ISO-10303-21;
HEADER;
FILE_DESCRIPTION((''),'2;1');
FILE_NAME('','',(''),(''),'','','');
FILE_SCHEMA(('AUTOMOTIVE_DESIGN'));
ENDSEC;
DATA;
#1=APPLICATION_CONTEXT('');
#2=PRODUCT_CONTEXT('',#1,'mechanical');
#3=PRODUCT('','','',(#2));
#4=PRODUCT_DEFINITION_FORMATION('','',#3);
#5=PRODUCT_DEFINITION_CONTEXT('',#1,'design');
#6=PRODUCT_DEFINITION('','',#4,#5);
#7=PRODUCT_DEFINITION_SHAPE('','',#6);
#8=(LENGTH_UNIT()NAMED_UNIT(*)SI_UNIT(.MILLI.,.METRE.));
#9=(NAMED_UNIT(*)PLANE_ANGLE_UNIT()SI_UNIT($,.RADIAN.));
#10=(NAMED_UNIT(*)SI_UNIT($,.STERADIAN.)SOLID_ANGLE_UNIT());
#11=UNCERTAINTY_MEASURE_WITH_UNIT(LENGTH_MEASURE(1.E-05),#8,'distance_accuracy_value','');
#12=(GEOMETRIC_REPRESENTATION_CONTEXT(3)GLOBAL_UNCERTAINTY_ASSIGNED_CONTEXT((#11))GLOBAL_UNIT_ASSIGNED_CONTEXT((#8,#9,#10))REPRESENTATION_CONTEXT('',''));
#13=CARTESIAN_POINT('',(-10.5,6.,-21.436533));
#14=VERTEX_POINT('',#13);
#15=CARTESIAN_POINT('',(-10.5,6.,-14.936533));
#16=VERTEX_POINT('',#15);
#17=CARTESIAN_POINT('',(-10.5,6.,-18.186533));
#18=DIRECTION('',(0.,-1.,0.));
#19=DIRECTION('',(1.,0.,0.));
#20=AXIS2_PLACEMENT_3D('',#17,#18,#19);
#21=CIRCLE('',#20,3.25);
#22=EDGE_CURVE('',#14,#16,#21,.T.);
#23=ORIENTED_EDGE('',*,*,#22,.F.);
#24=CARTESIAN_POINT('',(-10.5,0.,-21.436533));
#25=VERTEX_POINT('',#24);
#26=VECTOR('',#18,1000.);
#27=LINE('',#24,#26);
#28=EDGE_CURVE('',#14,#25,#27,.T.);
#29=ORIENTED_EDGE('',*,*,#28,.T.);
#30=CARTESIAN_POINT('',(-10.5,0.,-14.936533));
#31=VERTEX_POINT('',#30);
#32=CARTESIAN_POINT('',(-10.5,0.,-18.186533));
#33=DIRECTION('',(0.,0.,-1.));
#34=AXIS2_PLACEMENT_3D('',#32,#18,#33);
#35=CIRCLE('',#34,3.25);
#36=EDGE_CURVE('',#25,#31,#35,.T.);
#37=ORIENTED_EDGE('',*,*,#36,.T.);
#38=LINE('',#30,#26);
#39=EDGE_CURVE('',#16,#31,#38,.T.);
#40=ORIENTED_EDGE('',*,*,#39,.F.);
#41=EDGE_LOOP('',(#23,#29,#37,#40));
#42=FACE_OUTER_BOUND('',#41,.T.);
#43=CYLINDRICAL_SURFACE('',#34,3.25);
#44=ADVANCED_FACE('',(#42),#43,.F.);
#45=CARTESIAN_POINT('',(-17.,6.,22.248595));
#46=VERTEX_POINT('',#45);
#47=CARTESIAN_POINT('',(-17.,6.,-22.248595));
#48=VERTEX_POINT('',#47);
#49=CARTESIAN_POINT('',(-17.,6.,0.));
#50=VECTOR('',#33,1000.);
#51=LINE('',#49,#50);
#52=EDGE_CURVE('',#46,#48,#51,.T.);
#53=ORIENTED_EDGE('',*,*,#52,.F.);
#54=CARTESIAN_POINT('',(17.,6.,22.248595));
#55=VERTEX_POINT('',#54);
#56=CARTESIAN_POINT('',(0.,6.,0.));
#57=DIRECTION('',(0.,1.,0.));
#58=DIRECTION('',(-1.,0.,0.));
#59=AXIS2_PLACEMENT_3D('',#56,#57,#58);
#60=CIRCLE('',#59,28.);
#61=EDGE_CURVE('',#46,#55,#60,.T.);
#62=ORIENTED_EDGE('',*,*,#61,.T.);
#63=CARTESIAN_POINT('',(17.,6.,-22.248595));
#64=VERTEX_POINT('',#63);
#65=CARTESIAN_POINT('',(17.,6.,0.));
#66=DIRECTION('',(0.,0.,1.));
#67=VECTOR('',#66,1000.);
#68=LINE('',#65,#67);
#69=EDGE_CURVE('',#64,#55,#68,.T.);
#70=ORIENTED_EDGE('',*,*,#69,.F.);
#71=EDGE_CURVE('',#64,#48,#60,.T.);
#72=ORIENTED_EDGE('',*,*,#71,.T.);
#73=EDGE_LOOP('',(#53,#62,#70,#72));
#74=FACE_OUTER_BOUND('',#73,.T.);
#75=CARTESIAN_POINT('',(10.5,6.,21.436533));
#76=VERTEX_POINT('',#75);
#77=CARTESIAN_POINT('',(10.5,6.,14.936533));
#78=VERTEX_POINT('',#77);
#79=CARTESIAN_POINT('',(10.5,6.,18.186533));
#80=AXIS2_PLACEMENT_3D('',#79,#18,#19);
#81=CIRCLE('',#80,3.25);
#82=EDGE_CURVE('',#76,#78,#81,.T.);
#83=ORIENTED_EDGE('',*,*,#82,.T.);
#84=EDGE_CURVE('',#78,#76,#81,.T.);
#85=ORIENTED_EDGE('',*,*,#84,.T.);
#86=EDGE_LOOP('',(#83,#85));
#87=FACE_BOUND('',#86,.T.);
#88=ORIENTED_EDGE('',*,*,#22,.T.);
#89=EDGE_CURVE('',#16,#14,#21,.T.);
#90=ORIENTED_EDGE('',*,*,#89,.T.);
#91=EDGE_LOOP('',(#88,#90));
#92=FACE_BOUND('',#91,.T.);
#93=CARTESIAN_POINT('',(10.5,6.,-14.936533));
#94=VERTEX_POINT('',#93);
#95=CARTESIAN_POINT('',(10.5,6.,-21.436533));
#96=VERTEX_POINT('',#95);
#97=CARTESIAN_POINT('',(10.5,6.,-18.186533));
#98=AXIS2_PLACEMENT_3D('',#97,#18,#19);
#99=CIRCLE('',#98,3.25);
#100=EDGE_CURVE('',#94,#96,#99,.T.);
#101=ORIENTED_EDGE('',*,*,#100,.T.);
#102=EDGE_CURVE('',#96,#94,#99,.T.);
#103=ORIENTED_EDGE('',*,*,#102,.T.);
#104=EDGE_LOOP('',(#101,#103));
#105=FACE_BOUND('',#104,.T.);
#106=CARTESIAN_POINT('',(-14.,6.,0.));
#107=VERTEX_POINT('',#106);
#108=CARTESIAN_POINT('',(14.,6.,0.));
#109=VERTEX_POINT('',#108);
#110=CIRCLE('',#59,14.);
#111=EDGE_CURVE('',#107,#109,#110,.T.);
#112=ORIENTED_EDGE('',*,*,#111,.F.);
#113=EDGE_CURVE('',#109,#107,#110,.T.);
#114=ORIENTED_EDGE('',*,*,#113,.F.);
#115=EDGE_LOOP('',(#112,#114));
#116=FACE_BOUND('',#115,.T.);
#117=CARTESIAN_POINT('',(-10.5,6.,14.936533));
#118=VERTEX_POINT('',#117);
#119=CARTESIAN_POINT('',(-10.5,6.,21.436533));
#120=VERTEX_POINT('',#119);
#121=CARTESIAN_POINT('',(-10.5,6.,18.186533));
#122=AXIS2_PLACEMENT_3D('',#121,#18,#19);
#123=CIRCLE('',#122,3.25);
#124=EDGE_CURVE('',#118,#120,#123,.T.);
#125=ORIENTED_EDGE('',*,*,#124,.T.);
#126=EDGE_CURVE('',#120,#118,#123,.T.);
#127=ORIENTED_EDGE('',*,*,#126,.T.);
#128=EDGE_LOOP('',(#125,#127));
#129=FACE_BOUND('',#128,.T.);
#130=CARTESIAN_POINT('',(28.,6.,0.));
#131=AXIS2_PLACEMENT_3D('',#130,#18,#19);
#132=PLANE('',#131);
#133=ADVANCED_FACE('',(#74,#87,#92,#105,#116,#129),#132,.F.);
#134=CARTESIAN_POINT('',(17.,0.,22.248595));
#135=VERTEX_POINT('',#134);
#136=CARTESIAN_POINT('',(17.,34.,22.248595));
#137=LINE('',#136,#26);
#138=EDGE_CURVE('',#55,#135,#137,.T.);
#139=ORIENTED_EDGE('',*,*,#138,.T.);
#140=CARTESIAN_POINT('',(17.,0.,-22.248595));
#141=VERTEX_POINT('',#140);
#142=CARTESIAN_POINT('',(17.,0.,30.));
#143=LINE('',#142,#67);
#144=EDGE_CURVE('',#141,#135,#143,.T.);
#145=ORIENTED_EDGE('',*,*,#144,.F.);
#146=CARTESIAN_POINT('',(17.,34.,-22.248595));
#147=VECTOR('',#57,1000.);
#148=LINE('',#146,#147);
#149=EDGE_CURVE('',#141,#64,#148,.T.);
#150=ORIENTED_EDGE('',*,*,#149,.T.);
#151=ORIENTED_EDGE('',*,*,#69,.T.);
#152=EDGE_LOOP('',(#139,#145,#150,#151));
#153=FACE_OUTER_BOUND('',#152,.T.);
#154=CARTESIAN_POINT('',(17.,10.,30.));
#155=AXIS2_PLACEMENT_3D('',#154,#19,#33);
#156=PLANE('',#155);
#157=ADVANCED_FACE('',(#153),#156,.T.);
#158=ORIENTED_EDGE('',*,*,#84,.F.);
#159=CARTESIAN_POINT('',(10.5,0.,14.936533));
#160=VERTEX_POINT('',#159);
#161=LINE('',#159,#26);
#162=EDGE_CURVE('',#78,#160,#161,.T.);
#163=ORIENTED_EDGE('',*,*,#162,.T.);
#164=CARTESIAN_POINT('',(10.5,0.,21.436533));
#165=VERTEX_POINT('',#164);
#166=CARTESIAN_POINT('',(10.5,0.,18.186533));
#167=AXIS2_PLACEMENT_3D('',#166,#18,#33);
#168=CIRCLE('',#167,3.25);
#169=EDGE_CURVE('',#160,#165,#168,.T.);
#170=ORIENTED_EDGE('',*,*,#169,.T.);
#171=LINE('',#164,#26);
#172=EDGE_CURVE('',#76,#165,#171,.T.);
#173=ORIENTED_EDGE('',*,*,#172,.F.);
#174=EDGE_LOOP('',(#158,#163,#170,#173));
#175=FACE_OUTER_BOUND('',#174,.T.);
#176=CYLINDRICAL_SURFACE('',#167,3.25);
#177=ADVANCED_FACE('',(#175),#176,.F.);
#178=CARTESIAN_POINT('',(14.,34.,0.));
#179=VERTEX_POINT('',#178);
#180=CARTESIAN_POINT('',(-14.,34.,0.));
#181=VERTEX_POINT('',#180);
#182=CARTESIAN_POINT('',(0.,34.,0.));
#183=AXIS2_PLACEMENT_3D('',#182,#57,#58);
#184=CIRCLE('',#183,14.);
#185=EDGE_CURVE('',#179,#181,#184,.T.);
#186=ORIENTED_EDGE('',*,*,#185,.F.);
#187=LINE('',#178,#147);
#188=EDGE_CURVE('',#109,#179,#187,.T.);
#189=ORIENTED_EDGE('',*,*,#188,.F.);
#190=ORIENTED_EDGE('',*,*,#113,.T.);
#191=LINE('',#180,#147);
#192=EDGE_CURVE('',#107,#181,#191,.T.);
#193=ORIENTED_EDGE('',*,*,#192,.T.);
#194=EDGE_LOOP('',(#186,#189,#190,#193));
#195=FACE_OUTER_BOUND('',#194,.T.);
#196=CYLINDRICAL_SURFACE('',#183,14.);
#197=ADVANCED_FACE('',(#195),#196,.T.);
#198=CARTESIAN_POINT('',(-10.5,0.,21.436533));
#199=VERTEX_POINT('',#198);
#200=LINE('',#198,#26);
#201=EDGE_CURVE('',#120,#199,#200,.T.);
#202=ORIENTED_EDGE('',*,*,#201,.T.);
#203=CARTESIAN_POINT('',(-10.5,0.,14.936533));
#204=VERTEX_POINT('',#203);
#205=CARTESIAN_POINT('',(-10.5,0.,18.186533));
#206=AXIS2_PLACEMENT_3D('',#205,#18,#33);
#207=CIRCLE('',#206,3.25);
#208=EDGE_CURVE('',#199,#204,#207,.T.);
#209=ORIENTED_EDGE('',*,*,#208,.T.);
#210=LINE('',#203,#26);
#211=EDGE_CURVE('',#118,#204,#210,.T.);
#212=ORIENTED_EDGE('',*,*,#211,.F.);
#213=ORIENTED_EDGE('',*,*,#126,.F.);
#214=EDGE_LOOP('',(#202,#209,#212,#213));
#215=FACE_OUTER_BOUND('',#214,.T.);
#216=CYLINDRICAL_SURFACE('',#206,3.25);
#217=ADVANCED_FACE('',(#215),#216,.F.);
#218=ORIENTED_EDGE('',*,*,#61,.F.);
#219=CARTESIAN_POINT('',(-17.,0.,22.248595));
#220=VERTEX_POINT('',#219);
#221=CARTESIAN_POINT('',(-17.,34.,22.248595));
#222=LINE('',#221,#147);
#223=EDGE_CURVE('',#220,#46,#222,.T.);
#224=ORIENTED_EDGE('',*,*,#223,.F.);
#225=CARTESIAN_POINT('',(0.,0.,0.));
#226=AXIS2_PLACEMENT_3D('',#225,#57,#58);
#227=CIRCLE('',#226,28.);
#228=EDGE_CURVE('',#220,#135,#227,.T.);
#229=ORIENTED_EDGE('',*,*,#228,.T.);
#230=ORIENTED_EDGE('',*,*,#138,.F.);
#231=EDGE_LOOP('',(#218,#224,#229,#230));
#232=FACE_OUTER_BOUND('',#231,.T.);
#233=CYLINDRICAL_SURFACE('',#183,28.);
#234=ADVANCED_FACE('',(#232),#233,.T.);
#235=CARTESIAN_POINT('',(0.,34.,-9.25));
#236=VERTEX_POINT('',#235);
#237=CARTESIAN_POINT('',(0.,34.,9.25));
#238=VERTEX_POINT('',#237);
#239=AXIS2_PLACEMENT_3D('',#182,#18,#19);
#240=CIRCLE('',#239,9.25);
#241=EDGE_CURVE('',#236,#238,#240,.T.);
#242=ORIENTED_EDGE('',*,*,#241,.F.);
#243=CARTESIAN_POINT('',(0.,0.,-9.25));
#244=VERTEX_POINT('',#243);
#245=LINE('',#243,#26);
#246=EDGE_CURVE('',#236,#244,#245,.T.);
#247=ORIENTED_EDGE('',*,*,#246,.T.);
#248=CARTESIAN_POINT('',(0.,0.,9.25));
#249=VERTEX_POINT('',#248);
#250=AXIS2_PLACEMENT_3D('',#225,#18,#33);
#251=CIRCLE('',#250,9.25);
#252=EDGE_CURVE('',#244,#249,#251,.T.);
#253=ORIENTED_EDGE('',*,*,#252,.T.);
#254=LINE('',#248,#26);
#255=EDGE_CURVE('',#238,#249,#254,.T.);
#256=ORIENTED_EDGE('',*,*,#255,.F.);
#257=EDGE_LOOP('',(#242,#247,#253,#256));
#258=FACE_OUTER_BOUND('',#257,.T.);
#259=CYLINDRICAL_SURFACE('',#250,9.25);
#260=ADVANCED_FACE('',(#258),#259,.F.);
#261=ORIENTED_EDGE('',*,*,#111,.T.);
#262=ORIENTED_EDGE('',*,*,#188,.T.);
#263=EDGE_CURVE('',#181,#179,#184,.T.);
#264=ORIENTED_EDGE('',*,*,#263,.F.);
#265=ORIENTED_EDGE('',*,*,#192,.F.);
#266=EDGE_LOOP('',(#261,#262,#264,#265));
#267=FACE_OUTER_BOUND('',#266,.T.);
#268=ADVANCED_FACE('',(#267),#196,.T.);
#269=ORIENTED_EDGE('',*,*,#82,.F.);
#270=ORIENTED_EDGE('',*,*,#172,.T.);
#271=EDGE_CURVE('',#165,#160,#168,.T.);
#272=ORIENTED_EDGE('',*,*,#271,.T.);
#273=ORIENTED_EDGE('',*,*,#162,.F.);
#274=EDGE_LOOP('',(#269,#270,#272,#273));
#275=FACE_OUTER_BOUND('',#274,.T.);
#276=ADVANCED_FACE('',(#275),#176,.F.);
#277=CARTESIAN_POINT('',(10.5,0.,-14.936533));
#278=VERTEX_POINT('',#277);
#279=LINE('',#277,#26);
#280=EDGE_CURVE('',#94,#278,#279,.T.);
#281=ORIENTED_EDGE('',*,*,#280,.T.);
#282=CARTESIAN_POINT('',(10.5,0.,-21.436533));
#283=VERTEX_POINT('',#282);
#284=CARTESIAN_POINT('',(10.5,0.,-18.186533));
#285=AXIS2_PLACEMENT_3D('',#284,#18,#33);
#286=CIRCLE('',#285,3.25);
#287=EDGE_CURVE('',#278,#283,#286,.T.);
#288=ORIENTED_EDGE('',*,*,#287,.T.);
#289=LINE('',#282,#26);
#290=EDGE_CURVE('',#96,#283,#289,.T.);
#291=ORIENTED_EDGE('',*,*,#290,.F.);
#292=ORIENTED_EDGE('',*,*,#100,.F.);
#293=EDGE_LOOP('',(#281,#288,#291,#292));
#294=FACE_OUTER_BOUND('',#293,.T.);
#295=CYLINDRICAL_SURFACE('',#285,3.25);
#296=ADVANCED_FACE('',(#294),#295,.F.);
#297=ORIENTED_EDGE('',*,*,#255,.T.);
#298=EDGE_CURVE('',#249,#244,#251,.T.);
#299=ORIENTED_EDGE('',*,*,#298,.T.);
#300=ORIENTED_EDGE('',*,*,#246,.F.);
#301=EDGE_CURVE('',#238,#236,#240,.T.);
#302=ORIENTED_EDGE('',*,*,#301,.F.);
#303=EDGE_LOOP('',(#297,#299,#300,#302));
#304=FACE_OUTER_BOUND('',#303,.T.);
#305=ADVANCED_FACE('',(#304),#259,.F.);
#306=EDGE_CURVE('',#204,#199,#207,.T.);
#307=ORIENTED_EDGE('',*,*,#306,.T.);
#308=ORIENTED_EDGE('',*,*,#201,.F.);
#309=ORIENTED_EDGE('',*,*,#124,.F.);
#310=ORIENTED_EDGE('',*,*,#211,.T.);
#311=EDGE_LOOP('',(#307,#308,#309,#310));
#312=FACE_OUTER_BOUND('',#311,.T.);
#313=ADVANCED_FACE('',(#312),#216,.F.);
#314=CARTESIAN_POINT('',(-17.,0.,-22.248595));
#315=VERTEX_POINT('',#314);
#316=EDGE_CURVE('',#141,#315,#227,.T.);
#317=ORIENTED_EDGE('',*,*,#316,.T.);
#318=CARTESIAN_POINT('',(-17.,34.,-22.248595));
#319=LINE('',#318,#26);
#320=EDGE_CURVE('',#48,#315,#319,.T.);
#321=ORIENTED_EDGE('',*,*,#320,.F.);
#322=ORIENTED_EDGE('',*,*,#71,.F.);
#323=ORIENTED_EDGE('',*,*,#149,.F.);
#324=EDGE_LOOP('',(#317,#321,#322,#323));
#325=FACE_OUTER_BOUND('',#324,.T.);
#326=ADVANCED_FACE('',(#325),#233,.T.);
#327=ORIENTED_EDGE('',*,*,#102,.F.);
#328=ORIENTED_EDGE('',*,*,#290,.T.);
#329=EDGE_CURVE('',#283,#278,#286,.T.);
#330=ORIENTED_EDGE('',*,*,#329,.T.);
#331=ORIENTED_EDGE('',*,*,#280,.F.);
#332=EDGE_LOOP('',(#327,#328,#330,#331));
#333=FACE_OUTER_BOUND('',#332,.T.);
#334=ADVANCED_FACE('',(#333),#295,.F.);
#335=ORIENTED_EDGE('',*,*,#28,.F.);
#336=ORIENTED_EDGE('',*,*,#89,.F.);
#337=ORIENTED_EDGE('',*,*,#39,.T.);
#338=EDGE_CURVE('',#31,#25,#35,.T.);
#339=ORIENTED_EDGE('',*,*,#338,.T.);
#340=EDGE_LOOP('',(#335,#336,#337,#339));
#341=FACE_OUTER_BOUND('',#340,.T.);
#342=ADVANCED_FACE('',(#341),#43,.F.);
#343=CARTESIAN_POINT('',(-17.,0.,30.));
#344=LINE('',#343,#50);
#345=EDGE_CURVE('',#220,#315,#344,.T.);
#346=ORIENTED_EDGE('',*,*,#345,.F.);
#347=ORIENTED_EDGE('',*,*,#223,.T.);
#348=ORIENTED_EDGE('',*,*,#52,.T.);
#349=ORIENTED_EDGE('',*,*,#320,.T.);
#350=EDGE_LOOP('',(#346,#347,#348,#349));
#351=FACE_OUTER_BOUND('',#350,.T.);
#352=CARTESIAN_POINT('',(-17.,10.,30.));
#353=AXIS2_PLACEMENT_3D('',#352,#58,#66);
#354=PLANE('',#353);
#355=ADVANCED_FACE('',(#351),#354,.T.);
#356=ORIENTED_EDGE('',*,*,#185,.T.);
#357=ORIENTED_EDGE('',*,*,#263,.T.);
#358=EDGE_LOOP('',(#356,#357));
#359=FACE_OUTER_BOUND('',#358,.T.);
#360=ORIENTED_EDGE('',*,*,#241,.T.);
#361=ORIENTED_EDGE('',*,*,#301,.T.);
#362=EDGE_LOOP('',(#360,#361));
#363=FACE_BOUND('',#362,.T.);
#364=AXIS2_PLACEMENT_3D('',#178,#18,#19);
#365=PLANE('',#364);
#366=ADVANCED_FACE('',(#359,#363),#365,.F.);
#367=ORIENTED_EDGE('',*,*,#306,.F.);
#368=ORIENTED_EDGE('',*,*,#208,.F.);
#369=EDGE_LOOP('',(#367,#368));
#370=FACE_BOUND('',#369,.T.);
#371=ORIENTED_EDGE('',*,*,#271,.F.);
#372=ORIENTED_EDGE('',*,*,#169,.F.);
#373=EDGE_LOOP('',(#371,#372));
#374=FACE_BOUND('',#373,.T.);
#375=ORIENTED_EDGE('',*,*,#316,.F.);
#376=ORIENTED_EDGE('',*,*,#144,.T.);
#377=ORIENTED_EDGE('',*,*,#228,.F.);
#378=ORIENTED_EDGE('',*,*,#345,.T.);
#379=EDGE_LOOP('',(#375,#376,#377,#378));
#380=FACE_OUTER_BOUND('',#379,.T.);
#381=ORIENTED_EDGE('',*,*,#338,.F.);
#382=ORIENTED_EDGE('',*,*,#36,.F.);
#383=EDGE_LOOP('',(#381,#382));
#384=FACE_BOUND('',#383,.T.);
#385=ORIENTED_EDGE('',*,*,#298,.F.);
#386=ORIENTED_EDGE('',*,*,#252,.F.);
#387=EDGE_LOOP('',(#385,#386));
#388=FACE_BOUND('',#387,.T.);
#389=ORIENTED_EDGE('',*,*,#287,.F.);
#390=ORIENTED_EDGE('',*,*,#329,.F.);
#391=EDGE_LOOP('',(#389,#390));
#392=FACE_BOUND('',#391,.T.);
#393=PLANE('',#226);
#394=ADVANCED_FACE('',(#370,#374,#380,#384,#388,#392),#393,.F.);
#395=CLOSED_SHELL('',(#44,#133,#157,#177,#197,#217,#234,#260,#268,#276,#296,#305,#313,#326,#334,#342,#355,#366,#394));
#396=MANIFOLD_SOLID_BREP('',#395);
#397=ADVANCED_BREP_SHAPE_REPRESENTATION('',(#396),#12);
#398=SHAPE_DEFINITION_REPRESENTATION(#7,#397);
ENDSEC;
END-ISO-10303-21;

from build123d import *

# Parameters (mm, degrees)
SKETCH2_OUTSIDE_W              = 75.238
SKETCH2_OUTSIDE_H              = 75.238
SKETCH2_OUTSIDE_W_2            = 34
SKETCH2_OUTSIDE_H_2            = 60
CUT_EXTRUDE1_DEPTH             = 10
F_6_5_6_5_DIAMETER_HOLE1_D     = 6.5
F_6_5_6_5_DIAMETER_HOLE1_DEPTH = 20
F_6_5_6_5_DIAMETER_HOLE1_TIP   = 1.952797012
M20X1_5_TAPPED_HOLE1_D         = 18.5
M20X1_5_TAPPED_HOLE1_DEPTH     = 44.5
M20X1_5_TAPPED_HOLE1_TIP       = 5.557960726


with BuildPart() as part:
    # Sketch1 → Revolve1 (revolve)
    with BuildSketch(Plane.XY, mode=Mode.PRIVATE) as revolve1_sk:
        Polygon((0, 0), (28, 0), (28, 6), (14, 6), (14, 34), (0, 34), align=None)
    revolve(revolve1_sk.sketch.rotate(Axis((0, 34, 0), (0, -1, 0)), 180), axis=Axis((0, 34, 0), (0, -1, 0)))

    # Sketch2 outside → Cut-Extrude1 (cut)
    with BuildSketch(Plane.XZ):
        Rectangle(SKETCH2_OUTSIDE_W, SKETCH2_OUTSIDE_H)
        Rectangle(SKETCH2_OUTSIDE_W_2, SKETCH2_OUTSIDE_H_2, mode=Mode.SUBTRACT)
    extrude(amount=-CUT_EXTRUDE1_DEPTH, mode=Mode.SUBTRACT)

    # Ø6.5 (6.5) Diameter Hole1
    with Locations(Plane.XZ):
        with Locations((-10.5, 18.186533479), (10.5, 18.186533479), (-10.5, -18.186533479), (10.5, -18.186533479)):
            Hole(F_6_5_6_5_DIAMETER_HOLE1_D / 2, depth=F_6_5_6_5_DIAMETER_HOLE1_DEPTH)
            with Locations((0, 0, -(F_6_5_6_5_DIAMETER_HOLE1_DEPTH + F_6_5_6_5_DIAMETER_HOLE1_TIP / 2))):  # 118° drill point
                Cone(0, F_6_5_6_5_DIAMETER_HOLE1_D / 2, F_6_5_6_5_DIAMETER_HOLE1_TIP, mode=Mode.SUBTRACT)

    # M20x1.5 Tapped Hole1
    with Locations(Plane.XZ):
        with Locations((0, 0)):
            Hole(M20X1_5_TAPPED_HOLE1_D / 2, depth=M20X1_5_TAPPED_HOLE1_DEPTH)
            with Locations((0, 0, -(M20X1_5_TAPPED_HOLE1_DEPTH + M20X1_5_TAPPED_HOLE1_TIP / 2))):  # 118° drill point
                Cone(0, M20X1_5_TAPPED_HOLE1_D / 2, M20X1_5_TAPPED_HOLE1_TIP, mode=Mode.SUBTRACT)


solid = part.part
